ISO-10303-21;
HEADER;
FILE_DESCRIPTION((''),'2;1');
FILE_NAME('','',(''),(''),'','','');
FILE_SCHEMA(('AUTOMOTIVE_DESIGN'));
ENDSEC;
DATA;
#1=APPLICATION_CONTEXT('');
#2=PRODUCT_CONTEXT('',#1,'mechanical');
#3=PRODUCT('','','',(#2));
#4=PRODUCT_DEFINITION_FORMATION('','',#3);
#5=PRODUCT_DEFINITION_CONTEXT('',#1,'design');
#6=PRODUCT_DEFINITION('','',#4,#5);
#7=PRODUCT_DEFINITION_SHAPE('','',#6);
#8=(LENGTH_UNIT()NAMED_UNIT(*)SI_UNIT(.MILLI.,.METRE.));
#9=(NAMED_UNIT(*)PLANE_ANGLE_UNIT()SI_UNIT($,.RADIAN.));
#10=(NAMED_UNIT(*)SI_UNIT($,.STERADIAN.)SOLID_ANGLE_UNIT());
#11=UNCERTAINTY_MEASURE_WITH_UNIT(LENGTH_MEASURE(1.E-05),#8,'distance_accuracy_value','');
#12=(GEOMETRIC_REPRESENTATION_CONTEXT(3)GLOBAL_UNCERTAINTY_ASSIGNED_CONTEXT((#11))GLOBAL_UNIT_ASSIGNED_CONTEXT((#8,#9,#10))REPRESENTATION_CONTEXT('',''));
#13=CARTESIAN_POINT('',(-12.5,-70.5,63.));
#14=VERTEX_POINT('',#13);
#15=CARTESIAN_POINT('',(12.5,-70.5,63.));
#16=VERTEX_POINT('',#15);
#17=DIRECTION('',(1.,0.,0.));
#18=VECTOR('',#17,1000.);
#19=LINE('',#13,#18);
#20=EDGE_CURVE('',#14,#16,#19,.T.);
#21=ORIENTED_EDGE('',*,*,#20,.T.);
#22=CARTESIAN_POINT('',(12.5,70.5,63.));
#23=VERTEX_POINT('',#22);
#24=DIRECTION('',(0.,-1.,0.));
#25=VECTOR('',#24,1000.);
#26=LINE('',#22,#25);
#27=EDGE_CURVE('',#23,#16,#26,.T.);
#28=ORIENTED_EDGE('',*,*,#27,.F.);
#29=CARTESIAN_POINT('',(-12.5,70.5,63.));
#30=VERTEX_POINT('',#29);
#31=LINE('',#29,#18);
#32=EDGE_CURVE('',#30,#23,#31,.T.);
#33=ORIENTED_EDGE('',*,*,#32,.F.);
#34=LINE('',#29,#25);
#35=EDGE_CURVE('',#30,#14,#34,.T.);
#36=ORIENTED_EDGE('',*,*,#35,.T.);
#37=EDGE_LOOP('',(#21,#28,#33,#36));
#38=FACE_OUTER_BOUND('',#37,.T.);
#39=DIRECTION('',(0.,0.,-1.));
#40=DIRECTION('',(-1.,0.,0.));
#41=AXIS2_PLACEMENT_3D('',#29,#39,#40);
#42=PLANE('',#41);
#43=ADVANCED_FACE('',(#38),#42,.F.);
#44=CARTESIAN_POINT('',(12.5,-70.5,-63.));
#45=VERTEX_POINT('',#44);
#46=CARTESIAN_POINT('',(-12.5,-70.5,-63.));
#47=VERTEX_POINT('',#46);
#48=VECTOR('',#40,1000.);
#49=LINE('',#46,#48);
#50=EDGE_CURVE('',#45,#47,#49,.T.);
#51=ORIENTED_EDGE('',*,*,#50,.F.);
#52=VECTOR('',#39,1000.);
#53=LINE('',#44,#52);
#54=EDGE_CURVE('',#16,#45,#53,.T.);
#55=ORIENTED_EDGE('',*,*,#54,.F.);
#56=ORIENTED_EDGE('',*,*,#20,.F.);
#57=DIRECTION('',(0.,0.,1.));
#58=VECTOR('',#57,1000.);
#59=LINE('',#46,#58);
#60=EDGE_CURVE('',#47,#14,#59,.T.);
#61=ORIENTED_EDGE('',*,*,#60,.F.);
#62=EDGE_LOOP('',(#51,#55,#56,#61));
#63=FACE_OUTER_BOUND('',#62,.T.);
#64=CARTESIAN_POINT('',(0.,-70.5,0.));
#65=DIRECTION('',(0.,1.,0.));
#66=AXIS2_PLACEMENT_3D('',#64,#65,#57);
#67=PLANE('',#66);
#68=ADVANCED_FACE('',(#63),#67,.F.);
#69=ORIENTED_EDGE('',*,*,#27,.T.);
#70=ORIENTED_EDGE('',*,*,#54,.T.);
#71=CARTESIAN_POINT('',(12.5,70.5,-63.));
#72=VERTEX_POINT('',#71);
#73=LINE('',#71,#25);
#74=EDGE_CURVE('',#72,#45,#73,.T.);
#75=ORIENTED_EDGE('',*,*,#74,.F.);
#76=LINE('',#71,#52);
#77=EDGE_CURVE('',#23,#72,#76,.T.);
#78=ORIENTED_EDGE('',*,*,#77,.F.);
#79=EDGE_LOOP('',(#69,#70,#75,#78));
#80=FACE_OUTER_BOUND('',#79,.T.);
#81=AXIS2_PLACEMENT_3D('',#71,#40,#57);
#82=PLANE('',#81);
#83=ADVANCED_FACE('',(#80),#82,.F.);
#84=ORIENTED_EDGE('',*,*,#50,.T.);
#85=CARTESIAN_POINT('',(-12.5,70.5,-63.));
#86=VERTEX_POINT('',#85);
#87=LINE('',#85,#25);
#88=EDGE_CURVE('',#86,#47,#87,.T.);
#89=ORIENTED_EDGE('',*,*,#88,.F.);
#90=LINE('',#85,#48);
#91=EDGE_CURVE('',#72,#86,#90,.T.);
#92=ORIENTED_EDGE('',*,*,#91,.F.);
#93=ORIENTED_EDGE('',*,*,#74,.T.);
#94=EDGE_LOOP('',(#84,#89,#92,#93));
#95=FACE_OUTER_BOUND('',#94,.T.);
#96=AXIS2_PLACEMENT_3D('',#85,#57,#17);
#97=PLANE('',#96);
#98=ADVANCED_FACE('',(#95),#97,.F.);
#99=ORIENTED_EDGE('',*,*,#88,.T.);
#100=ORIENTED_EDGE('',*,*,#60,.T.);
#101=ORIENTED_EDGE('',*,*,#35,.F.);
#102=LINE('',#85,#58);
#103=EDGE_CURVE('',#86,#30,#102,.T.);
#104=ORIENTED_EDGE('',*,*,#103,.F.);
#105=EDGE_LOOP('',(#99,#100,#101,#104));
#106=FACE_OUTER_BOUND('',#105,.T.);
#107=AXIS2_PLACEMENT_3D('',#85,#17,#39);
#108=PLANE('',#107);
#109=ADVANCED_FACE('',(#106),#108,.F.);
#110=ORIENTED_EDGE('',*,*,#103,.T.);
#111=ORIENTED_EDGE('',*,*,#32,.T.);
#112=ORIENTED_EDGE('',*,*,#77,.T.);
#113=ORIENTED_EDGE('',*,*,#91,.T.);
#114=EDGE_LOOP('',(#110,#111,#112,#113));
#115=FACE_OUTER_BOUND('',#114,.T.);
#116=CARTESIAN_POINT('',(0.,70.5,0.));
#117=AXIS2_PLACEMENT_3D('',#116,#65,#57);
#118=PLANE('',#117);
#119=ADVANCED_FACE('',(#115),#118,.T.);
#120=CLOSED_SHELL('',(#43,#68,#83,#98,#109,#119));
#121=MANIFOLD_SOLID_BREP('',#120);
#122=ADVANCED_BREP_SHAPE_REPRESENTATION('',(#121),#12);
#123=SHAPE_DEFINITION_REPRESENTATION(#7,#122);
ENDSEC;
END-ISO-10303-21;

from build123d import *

# Parameters (mm, degrees)
SKETCH2_W           = 25
SKETCH2_H           = 126
BOSS_EXTRUDE1_DEPTH = 70.5


with BuildPart() as part:
    # Sketch2 → Boss-Extrude1 (new, symmetric)
    with BuildSketch(Plane(origin=(0, 0, 0), x_dir=(1, 0, 0), z_dir=(0, 1, 0))):
        Rectangle(SKETCH2_W, SKETCH2_H)
    extrude(amount=BOSS_EXTRUDE1_DEPTH, both=True)


solid = part.part
